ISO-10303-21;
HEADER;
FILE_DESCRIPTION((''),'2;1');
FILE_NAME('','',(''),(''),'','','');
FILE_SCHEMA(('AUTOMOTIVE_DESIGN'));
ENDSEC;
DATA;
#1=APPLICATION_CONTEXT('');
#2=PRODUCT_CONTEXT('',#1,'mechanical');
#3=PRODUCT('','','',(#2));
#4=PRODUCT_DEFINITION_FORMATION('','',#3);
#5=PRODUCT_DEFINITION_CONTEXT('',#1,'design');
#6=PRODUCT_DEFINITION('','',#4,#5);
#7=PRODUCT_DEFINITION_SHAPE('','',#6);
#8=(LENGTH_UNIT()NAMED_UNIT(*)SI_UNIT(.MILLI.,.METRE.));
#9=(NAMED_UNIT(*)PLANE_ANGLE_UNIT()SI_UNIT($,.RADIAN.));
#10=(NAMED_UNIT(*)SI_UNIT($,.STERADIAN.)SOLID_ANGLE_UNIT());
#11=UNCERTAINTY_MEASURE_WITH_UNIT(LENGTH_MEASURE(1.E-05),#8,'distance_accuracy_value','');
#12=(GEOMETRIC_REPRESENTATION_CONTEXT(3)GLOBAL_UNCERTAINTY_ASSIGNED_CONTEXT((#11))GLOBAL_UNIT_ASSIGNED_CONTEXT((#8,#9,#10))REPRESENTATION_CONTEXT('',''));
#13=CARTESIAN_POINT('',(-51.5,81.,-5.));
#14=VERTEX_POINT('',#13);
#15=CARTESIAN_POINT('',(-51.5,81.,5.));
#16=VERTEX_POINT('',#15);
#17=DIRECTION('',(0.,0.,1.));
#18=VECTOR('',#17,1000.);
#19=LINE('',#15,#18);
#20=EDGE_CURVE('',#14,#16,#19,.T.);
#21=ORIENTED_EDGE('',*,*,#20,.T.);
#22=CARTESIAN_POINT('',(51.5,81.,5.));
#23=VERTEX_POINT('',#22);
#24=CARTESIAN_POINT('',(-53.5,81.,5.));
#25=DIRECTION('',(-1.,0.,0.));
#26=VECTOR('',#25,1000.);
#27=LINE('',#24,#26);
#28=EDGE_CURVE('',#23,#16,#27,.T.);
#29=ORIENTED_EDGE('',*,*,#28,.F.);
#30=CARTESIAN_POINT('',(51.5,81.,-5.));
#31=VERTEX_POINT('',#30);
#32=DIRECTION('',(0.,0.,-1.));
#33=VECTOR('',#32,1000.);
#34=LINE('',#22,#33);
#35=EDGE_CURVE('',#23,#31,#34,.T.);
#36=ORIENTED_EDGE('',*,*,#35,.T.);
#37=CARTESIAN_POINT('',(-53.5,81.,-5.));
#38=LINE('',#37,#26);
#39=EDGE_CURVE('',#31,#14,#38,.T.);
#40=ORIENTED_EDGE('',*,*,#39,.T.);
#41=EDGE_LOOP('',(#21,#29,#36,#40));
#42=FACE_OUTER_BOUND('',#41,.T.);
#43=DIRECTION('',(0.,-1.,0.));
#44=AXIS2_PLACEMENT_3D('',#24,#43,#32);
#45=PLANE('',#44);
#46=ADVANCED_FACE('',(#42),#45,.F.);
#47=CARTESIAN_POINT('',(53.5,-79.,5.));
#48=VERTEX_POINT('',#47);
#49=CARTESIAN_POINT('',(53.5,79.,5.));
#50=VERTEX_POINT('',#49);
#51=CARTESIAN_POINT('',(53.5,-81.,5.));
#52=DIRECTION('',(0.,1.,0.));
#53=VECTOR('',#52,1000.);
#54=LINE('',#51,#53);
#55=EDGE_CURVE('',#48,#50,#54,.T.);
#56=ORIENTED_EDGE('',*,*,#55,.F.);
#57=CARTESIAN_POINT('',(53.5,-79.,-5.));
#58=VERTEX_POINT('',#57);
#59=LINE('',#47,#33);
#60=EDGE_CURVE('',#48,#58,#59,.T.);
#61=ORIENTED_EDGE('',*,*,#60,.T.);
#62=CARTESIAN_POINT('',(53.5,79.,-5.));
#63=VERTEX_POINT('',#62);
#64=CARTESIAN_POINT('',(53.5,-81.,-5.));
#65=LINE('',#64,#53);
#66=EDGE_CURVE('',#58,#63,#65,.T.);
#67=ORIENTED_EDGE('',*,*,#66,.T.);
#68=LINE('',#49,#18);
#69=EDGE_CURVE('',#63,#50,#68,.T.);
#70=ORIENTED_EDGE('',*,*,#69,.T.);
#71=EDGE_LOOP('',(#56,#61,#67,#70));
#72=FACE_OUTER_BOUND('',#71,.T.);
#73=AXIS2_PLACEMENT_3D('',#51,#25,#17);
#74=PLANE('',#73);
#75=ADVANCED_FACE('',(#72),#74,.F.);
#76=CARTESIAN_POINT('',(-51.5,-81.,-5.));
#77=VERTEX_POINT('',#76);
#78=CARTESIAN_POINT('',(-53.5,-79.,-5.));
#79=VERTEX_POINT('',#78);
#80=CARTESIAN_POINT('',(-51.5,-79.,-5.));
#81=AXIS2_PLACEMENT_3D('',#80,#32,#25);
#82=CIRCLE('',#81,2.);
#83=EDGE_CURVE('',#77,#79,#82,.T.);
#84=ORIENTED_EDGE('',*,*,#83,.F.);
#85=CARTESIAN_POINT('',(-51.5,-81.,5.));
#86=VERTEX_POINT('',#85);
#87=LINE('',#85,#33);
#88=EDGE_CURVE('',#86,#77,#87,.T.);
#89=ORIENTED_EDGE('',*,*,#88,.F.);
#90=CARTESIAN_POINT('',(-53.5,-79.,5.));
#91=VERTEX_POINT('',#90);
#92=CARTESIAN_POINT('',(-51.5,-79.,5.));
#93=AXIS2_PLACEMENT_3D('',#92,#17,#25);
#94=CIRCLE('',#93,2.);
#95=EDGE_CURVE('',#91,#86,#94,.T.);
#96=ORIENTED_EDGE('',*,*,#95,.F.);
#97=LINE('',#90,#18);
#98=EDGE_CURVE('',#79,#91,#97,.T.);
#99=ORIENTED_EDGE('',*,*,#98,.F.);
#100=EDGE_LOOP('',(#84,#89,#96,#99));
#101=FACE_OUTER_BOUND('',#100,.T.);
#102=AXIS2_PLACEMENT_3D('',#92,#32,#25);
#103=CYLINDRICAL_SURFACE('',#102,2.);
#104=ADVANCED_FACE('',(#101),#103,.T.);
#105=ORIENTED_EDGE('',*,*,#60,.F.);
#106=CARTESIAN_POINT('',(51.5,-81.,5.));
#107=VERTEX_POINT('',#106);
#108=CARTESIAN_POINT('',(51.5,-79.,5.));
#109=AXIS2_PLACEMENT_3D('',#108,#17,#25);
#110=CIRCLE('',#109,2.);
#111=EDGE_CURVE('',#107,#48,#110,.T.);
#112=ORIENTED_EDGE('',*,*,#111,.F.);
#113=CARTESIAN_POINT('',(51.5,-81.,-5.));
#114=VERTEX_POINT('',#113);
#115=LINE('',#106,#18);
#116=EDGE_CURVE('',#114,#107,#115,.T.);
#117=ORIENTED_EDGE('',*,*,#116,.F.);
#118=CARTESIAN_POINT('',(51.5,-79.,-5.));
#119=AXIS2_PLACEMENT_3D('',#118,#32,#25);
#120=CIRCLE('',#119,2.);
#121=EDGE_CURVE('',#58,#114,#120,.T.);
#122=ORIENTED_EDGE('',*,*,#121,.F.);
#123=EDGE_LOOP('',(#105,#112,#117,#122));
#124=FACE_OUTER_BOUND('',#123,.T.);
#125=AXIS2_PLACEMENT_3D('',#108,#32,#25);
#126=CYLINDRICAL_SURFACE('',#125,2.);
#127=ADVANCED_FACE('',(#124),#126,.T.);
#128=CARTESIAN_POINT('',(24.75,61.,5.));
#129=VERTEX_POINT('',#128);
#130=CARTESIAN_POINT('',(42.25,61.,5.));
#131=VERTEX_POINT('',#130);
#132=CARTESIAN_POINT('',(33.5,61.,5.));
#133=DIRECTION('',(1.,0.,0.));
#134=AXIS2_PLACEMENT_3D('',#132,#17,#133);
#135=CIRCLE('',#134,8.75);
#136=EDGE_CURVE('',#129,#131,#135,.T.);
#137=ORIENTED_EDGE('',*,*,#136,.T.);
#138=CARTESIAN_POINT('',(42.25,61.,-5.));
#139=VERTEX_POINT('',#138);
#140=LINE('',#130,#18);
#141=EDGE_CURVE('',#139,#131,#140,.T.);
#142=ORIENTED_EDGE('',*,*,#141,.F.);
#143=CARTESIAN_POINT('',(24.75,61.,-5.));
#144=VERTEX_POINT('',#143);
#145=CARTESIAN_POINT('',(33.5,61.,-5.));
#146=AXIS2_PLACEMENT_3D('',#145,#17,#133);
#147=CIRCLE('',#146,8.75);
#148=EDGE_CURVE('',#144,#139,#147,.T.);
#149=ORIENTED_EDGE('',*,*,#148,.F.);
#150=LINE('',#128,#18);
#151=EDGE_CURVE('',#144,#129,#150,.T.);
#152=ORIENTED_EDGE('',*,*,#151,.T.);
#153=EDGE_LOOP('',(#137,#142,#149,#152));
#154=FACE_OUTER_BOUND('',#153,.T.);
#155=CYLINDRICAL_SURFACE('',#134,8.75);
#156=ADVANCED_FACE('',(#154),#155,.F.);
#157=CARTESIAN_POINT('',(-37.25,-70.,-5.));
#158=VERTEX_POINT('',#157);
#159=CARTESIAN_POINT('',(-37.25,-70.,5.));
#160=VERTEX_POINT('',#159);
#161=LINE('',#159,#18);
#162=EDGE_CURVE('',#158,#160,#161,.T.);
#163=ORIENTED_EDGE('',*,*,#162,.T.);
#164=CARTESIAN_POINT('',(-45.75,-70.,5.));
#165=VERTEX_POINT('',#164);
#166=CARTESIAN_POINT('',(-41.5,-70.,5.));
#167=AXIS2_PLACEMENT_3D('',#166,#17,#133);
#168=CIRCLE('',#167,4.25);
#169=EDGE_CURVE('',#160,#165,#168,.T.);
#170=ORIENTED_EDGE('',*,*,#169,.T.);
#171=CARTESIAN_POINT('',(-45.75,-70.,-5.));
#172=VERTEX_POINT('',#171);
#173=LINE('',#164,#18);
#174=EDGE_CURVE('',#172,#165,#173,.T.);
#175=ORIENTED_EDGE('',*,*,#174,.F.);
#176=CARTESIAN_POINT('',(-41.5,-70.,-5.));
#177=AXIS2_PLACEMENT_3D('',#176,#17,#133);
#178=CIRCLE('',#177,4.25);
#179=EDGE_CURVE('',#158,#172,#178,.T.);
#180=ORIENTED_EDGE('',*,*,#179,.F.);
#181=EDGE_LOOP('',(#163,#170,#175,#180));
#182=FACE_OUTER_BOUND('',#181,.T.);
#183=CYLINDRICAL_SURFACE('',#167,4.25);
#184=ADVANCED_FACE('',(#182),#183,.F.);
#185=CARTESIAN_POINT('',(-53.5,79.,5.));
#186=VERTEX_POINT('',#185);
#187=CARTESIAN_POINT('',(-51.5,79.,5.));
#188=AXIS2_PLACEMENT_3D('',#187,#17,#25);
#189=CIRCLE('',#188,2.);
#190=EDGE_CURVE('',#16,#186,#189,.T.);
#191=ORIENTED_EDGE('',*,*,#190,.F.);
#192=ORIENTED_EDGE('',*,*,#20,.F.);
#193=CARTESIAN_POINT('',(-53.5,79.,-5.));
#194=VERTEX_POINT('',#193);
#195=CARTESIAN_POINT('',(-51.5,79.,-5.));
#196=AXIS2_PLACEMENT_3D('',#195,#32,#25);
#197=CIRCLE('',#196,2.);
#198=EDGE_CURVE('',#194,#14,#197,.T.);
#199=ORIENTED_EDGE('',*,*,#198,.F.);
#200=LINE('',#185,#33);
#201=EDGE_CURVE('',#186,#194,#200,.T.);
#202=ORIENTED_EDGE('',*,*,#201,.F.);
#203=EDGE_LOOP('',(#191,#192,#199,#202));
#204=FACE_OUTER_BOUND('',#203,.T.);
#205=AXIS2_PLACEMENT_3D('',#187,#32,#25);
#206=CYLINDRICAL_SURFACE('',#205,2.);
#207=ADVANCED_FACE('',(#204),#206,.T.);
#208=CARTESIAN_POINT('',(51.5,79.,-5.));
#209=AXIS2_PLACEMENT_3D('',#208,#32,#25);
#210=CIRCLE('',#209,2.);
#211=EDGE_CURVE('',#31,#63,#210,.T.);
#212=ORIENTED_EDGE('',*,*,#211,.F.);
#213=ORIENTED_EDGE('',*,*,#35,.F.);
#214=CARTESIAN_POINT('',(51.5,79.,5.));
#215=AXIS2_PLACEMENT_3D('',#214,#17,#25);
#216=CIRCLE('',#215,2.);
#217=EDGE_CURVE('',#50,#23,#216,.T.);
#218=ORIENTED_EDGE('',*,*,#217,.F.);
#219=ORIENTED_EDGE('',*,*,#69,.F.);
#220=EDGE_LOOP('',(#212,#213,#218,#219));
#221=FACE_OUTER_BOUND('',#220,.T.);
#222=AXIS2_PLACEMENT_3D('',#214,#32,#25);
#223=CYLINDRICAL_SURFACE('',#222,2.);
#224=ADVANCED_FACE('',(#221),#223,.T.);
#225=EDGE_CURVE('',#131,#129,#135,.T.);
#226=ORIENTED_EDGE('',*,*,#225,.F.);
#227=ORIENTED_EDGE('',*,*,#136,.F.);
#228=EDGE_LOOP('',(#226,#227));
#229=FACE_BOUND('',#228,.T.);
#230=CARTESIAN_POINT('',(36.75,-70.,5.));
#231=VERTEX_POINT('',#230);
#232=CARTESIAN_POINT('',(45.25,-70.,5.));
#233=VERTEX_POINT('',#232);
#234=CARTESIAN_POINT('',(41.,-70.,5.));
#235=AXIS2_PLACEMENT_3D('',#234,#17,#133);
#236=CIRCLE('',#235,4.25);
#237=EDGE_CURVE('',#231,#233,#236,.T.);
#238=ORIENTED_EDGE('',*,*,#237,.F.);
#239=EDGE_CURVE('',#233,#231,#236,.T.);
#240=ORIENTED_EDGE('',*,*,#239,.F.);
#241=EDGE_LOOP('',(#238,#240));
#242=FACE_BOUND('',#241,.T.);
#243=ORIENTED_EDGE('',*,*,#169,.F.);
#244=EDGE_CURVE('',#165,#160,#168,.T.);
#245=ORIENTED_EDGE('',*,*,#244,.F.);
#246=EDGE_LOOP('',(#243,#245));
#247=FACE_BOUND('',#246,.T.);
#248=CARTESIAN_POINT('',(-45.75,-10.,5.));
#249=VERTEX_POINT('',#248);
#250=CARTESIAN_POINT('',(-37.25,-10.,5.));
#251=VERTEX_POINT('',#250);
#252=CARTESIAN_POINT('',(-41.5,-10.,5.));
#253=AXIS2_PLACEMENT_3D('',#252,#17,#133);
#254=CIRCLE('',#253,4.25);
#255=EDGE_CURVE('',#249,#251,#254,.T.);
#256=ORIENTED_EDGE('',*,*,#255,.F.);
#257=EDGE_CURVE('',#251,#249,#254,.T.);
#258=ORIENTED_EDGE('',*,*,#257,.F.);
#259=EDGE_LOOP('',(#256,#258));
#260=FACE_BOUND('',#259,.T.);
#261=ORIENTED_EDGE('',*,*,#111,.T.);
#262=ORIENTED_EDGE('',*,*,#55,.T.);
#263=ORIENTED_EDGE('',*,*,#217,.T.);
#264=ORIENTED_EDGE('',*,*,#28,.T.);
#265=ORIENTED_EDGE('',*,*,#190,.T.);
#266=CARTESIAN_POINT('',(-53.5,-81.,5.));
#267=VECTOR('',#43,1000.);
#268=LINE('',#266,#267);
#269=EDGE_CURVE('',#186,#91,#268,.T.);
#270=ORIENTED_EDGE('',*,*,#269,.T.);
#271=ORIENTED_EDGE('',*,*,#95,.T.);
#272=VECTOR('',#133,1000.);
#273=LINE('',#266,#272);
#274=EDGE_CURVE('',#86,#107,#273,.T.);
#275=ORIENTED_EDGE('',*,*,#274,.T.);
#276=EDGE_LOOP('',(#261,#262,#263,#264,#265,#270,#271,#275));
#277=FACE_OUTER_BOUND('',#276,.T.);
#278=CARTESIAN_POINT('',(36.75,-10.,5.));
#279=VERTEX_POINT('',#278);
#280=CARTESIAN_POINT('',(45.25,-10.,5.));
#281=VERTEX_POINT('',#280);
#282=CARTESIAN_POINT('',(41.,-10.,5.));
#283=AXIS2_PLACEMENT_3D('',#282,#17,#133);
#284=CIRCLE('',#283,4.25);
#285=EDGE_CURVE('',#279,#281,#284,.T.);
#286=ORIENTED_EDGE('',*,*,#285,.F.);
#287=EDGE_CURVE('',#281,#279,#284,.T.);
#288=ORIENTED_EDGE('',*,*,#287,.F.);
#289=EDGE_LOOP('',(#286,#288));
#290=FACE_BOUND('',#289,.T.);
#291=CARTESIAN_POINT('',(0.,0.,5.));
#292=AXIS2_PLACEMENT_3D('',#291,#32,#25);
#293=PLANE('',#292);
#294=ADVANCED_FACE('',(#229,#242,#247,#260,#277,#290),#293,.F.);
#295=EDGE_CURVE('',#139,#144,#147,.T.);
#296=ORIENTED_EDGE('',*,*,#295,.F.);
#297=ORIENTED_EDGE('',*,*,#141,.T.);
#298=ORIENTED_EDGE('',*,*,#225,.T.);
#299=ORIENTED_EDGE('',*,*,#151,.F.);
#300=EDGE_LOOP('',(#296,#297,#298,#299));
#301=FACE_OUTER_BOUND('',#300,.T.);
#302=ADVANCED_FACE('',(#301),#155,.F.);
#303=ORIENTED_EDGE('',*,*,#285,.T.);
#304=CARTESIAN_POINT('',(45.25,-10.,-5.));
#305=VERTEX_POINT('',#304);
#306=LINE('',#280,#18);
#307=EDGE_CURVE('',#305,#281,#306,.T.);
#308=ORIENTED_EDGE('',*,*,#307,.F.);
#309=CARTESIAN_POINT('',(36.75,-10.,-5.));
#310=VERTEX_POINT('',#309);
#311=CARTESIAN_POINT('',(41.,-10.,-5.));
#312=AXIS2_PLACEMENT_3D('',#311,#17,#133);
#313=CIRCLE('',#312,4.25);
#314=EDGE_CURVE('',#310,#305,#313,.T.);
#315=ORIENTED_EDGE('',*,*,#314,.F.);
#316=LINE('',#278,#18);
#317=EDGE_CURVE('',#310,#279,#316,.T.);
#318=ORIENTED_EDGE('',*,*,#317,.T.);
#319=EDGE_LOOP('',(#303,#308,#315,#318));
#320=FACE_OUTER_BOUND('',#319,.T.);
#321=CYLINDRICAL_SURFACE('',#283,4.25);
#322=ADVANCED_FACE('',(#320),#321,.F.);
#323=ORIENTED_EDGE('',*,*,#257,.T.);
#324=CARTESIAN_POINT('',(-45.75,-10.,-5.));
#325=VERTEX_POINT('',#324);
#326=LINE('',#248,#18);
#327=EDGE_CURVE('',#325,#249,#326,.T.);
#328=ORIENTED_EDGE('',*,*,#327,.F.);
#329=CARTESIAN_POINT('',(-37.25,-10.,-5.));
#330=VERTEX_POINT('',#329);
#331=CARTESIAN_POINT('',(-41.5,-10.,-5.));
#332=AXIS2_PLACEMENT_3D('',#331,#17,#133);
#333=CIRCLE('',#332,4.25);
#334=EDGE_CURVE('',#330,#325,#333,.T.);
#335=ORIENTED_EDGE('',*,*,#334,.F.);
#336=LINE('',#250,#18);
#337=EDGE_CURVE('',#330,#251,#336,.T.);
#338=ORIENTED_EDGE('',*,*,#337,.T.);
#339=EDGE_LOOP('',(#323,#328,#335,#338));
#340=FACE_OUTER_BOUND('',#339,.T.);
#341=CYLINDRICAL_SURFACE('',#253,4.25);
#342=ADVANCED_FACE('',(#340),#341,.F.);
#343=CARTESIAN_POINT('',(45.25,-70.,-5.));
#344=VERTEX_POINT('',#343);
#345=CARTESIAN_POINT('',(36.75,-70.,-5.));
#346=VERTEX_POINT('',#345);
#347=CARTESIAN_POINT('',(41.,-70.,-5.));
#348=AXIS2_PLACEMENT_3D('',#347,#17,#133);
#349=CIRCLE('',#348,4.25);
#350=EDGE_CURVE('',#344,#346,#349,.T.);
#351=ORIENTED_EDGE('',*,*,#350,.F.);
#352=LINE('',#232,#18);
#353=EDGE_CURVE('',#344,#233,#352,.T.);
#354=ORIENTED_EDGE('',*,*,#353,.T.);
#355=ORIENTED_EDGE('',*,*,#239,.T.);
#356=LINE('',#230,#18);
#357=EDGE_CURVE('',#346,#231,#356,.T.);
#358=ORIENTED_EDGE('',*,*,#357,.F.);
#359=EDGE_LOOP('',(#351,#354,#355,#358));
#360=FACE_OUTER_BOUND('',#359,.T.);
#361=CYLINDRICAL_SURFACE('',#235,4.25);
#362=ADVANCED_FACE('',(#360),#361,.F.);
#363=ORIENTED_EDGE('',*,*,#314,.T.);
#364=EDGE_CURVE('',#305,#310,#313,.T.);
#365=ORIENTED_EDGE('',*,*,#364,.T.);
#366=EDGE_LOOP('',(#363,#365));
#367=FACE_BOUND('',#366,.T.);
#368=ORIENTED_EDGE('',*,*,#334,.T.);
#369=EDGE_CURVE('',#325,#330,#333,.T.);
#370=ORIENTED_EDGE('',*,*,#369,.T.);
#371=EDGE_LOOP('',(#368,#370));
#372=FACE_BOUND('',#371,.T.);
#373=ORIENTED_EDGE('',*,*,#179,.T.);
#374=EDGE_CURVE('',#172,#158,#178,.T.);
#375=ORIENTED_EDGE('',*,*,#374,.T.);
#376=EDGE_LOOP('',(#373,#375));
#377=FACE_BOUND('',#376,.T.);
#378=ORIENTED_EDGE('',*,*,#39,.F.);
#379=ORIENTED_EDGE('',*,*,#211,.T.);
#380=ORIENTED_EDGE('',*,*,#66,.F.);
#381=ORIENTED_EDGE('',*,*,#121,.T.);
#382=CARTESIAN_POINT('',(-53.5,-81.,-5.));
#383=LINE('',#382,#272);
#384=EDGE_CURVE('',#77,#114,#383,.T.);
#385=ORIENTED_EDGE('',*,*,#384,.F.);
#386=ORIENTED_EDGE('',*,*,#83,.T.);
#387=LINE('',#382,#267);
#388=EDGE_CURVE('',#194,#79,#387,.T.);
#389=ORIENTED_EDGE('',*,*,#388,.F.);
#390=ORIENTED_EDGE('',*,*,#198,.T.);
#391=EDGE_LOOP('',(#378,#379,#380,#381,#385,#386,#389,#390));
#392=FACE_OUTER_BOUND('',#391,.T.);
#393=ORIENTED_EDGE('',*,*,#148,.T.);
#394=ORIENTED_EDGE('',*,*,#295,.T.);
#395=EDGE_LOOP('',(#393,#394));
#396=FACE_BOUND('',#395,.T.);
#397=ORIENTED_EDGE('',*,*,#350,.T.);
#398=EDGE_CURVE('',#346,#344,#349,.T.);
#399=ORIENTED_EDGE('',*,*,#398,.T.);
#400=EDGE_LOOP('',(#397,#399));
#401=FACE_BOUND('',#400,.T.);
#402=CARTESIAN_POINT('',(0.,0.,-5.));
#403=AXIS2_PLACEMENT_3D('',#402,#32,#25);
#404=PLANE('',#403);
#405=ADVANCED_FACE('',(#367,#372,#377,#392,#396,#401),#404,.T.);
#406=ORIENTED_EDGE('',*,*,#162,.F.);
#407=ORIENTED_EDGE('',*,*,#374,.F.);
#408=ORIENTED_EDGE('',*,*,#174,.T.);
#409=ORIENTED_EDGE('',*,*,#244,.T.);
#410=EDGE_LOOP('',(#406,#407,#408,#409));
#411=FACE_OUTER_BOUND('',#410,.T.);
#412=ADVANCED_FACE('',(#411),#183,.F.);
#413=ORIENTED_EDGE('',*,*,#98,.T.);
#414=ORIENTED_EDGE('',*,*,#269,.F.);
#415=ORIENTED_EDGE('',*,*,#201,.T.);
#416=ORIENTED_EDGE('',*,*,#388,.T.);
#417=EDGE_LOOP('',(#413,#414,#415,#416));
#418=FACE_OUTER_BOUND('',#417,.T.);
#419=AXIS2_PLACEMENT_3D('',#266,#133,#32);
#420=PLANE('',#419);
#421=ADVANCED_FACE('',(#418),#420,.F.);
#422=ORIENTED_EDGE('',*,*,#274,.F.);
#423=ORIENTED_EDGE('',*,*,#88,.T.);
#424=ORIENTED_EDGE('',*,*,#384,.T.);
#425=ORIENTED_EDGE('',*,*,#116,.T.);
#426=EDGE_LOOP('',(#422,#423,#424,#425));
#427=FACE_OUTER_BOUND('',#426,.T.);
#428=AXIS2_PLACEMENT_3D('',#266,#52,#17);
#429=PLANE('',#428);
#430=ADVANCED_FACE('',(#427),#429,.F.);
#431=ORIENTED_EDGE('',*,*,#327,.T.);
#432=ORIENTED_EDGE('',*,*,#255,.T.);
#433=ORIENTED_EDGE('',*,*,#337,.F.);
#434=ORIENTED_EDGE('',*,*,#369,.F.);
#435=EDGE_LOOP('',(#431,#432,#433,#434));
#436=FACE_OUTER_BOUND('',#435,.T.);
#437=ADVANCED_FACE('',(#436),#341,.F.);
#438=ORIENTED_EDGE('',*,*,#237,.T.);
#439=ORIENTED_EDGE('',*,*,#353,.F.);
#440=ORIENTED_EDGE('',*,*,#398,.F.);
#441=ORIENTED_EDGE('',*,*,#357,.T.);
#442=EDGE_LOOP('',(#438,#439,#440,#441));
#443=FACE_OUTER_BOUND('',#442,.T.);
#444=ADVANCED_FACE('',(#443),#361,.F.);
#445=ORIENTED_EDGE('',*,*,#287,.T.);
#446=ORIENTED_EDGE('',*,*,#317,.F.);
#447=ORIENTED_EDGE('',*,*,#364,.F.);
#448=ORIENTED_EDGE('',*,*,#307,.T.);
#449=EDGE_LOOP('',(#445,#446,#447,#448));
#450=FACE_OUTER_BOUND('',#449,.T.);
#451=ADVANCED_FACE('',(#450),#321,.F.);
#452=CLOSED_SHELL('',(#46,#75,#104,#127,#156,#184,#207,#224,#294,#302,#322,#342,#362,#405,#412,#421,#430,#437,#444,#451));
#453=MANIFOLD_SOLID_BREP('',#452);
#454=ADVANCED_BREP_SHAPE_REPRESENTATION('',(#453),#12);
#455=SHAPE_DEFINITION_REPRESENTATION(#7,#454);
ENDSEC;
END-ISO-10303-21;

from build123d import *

# Parameters (mm, degrees)
SKETCH_1_W                  = 107
SKETCH_1_H                  = 162
EXTRUDE_1_DEPTH             = 5
HOLE_WIZARD_M20_1_D         = 17.5
FILLET_1_R                  = 2
HOLE_WIZARD_M10_1_D         = 8.5
PATTERN_LINEAR_1_COUNT      = 2
PATTERN_LINEAR_1_PITCH      = 82.5
PATTERN_LINEAR_1_COUNT_DIR2 = 2
PATTERN_LINEAR_1_PITCH_DIR2 = 60


with BuildPart() as part:
    # 草图1 → 凸台-拉伸1 (new, symmetric)
    with BuildSketch(Plane.XY):
        Rectangle(SKETCH_1_W, SKETCH_1_H)
    extrude(amount=EXTRUDE_1_DEPTH, both=True)

    # M20 螺纹孔1 (through all)
    with Locations(Plane.XY.offset(5)):
        with Locations((33.5, 61)):
            Hole(HOLE_WIZARD_M20_1_D / 2)

    # 圆角1
    fillet_1_edges = [part.edges().sort_by_distance(p)[0] for p in [
        (53.5, -81, 0),
        (-53.5, -81, 0),
        (-53.5, 81, 0),
        (53.5, 81, 0),
    ]]
    fillet(fillet_1_edges, radius=FILLET_1_R)

    # M10 螺纹孔1 (through all)
    with Locations(Plane.XY.offset(5)):
        with Locations((-41.5, -70)):
            hole_wizard_m10_1 = Hole(HOLE_WIZARD_M10_1_D / 2)

    # 阵列(线性)1: Hole Wizard M10 _1 2 × 2
    with Locations(*[(i * PATTERN_LINEAR_1_PITCH, j * PATTERN_LINEAR_1_PITCH_DIR2, 0) for i in range(PATTERN_LINEAR_1_COUNT) for j in range(PATTERN_LINEAR_1_COUNT_DIR2) if (i, j) != (0, 0)]):
        add(hole_wizard_m10_1, mode=Mode.SUBTRACT)


solid = part.part
